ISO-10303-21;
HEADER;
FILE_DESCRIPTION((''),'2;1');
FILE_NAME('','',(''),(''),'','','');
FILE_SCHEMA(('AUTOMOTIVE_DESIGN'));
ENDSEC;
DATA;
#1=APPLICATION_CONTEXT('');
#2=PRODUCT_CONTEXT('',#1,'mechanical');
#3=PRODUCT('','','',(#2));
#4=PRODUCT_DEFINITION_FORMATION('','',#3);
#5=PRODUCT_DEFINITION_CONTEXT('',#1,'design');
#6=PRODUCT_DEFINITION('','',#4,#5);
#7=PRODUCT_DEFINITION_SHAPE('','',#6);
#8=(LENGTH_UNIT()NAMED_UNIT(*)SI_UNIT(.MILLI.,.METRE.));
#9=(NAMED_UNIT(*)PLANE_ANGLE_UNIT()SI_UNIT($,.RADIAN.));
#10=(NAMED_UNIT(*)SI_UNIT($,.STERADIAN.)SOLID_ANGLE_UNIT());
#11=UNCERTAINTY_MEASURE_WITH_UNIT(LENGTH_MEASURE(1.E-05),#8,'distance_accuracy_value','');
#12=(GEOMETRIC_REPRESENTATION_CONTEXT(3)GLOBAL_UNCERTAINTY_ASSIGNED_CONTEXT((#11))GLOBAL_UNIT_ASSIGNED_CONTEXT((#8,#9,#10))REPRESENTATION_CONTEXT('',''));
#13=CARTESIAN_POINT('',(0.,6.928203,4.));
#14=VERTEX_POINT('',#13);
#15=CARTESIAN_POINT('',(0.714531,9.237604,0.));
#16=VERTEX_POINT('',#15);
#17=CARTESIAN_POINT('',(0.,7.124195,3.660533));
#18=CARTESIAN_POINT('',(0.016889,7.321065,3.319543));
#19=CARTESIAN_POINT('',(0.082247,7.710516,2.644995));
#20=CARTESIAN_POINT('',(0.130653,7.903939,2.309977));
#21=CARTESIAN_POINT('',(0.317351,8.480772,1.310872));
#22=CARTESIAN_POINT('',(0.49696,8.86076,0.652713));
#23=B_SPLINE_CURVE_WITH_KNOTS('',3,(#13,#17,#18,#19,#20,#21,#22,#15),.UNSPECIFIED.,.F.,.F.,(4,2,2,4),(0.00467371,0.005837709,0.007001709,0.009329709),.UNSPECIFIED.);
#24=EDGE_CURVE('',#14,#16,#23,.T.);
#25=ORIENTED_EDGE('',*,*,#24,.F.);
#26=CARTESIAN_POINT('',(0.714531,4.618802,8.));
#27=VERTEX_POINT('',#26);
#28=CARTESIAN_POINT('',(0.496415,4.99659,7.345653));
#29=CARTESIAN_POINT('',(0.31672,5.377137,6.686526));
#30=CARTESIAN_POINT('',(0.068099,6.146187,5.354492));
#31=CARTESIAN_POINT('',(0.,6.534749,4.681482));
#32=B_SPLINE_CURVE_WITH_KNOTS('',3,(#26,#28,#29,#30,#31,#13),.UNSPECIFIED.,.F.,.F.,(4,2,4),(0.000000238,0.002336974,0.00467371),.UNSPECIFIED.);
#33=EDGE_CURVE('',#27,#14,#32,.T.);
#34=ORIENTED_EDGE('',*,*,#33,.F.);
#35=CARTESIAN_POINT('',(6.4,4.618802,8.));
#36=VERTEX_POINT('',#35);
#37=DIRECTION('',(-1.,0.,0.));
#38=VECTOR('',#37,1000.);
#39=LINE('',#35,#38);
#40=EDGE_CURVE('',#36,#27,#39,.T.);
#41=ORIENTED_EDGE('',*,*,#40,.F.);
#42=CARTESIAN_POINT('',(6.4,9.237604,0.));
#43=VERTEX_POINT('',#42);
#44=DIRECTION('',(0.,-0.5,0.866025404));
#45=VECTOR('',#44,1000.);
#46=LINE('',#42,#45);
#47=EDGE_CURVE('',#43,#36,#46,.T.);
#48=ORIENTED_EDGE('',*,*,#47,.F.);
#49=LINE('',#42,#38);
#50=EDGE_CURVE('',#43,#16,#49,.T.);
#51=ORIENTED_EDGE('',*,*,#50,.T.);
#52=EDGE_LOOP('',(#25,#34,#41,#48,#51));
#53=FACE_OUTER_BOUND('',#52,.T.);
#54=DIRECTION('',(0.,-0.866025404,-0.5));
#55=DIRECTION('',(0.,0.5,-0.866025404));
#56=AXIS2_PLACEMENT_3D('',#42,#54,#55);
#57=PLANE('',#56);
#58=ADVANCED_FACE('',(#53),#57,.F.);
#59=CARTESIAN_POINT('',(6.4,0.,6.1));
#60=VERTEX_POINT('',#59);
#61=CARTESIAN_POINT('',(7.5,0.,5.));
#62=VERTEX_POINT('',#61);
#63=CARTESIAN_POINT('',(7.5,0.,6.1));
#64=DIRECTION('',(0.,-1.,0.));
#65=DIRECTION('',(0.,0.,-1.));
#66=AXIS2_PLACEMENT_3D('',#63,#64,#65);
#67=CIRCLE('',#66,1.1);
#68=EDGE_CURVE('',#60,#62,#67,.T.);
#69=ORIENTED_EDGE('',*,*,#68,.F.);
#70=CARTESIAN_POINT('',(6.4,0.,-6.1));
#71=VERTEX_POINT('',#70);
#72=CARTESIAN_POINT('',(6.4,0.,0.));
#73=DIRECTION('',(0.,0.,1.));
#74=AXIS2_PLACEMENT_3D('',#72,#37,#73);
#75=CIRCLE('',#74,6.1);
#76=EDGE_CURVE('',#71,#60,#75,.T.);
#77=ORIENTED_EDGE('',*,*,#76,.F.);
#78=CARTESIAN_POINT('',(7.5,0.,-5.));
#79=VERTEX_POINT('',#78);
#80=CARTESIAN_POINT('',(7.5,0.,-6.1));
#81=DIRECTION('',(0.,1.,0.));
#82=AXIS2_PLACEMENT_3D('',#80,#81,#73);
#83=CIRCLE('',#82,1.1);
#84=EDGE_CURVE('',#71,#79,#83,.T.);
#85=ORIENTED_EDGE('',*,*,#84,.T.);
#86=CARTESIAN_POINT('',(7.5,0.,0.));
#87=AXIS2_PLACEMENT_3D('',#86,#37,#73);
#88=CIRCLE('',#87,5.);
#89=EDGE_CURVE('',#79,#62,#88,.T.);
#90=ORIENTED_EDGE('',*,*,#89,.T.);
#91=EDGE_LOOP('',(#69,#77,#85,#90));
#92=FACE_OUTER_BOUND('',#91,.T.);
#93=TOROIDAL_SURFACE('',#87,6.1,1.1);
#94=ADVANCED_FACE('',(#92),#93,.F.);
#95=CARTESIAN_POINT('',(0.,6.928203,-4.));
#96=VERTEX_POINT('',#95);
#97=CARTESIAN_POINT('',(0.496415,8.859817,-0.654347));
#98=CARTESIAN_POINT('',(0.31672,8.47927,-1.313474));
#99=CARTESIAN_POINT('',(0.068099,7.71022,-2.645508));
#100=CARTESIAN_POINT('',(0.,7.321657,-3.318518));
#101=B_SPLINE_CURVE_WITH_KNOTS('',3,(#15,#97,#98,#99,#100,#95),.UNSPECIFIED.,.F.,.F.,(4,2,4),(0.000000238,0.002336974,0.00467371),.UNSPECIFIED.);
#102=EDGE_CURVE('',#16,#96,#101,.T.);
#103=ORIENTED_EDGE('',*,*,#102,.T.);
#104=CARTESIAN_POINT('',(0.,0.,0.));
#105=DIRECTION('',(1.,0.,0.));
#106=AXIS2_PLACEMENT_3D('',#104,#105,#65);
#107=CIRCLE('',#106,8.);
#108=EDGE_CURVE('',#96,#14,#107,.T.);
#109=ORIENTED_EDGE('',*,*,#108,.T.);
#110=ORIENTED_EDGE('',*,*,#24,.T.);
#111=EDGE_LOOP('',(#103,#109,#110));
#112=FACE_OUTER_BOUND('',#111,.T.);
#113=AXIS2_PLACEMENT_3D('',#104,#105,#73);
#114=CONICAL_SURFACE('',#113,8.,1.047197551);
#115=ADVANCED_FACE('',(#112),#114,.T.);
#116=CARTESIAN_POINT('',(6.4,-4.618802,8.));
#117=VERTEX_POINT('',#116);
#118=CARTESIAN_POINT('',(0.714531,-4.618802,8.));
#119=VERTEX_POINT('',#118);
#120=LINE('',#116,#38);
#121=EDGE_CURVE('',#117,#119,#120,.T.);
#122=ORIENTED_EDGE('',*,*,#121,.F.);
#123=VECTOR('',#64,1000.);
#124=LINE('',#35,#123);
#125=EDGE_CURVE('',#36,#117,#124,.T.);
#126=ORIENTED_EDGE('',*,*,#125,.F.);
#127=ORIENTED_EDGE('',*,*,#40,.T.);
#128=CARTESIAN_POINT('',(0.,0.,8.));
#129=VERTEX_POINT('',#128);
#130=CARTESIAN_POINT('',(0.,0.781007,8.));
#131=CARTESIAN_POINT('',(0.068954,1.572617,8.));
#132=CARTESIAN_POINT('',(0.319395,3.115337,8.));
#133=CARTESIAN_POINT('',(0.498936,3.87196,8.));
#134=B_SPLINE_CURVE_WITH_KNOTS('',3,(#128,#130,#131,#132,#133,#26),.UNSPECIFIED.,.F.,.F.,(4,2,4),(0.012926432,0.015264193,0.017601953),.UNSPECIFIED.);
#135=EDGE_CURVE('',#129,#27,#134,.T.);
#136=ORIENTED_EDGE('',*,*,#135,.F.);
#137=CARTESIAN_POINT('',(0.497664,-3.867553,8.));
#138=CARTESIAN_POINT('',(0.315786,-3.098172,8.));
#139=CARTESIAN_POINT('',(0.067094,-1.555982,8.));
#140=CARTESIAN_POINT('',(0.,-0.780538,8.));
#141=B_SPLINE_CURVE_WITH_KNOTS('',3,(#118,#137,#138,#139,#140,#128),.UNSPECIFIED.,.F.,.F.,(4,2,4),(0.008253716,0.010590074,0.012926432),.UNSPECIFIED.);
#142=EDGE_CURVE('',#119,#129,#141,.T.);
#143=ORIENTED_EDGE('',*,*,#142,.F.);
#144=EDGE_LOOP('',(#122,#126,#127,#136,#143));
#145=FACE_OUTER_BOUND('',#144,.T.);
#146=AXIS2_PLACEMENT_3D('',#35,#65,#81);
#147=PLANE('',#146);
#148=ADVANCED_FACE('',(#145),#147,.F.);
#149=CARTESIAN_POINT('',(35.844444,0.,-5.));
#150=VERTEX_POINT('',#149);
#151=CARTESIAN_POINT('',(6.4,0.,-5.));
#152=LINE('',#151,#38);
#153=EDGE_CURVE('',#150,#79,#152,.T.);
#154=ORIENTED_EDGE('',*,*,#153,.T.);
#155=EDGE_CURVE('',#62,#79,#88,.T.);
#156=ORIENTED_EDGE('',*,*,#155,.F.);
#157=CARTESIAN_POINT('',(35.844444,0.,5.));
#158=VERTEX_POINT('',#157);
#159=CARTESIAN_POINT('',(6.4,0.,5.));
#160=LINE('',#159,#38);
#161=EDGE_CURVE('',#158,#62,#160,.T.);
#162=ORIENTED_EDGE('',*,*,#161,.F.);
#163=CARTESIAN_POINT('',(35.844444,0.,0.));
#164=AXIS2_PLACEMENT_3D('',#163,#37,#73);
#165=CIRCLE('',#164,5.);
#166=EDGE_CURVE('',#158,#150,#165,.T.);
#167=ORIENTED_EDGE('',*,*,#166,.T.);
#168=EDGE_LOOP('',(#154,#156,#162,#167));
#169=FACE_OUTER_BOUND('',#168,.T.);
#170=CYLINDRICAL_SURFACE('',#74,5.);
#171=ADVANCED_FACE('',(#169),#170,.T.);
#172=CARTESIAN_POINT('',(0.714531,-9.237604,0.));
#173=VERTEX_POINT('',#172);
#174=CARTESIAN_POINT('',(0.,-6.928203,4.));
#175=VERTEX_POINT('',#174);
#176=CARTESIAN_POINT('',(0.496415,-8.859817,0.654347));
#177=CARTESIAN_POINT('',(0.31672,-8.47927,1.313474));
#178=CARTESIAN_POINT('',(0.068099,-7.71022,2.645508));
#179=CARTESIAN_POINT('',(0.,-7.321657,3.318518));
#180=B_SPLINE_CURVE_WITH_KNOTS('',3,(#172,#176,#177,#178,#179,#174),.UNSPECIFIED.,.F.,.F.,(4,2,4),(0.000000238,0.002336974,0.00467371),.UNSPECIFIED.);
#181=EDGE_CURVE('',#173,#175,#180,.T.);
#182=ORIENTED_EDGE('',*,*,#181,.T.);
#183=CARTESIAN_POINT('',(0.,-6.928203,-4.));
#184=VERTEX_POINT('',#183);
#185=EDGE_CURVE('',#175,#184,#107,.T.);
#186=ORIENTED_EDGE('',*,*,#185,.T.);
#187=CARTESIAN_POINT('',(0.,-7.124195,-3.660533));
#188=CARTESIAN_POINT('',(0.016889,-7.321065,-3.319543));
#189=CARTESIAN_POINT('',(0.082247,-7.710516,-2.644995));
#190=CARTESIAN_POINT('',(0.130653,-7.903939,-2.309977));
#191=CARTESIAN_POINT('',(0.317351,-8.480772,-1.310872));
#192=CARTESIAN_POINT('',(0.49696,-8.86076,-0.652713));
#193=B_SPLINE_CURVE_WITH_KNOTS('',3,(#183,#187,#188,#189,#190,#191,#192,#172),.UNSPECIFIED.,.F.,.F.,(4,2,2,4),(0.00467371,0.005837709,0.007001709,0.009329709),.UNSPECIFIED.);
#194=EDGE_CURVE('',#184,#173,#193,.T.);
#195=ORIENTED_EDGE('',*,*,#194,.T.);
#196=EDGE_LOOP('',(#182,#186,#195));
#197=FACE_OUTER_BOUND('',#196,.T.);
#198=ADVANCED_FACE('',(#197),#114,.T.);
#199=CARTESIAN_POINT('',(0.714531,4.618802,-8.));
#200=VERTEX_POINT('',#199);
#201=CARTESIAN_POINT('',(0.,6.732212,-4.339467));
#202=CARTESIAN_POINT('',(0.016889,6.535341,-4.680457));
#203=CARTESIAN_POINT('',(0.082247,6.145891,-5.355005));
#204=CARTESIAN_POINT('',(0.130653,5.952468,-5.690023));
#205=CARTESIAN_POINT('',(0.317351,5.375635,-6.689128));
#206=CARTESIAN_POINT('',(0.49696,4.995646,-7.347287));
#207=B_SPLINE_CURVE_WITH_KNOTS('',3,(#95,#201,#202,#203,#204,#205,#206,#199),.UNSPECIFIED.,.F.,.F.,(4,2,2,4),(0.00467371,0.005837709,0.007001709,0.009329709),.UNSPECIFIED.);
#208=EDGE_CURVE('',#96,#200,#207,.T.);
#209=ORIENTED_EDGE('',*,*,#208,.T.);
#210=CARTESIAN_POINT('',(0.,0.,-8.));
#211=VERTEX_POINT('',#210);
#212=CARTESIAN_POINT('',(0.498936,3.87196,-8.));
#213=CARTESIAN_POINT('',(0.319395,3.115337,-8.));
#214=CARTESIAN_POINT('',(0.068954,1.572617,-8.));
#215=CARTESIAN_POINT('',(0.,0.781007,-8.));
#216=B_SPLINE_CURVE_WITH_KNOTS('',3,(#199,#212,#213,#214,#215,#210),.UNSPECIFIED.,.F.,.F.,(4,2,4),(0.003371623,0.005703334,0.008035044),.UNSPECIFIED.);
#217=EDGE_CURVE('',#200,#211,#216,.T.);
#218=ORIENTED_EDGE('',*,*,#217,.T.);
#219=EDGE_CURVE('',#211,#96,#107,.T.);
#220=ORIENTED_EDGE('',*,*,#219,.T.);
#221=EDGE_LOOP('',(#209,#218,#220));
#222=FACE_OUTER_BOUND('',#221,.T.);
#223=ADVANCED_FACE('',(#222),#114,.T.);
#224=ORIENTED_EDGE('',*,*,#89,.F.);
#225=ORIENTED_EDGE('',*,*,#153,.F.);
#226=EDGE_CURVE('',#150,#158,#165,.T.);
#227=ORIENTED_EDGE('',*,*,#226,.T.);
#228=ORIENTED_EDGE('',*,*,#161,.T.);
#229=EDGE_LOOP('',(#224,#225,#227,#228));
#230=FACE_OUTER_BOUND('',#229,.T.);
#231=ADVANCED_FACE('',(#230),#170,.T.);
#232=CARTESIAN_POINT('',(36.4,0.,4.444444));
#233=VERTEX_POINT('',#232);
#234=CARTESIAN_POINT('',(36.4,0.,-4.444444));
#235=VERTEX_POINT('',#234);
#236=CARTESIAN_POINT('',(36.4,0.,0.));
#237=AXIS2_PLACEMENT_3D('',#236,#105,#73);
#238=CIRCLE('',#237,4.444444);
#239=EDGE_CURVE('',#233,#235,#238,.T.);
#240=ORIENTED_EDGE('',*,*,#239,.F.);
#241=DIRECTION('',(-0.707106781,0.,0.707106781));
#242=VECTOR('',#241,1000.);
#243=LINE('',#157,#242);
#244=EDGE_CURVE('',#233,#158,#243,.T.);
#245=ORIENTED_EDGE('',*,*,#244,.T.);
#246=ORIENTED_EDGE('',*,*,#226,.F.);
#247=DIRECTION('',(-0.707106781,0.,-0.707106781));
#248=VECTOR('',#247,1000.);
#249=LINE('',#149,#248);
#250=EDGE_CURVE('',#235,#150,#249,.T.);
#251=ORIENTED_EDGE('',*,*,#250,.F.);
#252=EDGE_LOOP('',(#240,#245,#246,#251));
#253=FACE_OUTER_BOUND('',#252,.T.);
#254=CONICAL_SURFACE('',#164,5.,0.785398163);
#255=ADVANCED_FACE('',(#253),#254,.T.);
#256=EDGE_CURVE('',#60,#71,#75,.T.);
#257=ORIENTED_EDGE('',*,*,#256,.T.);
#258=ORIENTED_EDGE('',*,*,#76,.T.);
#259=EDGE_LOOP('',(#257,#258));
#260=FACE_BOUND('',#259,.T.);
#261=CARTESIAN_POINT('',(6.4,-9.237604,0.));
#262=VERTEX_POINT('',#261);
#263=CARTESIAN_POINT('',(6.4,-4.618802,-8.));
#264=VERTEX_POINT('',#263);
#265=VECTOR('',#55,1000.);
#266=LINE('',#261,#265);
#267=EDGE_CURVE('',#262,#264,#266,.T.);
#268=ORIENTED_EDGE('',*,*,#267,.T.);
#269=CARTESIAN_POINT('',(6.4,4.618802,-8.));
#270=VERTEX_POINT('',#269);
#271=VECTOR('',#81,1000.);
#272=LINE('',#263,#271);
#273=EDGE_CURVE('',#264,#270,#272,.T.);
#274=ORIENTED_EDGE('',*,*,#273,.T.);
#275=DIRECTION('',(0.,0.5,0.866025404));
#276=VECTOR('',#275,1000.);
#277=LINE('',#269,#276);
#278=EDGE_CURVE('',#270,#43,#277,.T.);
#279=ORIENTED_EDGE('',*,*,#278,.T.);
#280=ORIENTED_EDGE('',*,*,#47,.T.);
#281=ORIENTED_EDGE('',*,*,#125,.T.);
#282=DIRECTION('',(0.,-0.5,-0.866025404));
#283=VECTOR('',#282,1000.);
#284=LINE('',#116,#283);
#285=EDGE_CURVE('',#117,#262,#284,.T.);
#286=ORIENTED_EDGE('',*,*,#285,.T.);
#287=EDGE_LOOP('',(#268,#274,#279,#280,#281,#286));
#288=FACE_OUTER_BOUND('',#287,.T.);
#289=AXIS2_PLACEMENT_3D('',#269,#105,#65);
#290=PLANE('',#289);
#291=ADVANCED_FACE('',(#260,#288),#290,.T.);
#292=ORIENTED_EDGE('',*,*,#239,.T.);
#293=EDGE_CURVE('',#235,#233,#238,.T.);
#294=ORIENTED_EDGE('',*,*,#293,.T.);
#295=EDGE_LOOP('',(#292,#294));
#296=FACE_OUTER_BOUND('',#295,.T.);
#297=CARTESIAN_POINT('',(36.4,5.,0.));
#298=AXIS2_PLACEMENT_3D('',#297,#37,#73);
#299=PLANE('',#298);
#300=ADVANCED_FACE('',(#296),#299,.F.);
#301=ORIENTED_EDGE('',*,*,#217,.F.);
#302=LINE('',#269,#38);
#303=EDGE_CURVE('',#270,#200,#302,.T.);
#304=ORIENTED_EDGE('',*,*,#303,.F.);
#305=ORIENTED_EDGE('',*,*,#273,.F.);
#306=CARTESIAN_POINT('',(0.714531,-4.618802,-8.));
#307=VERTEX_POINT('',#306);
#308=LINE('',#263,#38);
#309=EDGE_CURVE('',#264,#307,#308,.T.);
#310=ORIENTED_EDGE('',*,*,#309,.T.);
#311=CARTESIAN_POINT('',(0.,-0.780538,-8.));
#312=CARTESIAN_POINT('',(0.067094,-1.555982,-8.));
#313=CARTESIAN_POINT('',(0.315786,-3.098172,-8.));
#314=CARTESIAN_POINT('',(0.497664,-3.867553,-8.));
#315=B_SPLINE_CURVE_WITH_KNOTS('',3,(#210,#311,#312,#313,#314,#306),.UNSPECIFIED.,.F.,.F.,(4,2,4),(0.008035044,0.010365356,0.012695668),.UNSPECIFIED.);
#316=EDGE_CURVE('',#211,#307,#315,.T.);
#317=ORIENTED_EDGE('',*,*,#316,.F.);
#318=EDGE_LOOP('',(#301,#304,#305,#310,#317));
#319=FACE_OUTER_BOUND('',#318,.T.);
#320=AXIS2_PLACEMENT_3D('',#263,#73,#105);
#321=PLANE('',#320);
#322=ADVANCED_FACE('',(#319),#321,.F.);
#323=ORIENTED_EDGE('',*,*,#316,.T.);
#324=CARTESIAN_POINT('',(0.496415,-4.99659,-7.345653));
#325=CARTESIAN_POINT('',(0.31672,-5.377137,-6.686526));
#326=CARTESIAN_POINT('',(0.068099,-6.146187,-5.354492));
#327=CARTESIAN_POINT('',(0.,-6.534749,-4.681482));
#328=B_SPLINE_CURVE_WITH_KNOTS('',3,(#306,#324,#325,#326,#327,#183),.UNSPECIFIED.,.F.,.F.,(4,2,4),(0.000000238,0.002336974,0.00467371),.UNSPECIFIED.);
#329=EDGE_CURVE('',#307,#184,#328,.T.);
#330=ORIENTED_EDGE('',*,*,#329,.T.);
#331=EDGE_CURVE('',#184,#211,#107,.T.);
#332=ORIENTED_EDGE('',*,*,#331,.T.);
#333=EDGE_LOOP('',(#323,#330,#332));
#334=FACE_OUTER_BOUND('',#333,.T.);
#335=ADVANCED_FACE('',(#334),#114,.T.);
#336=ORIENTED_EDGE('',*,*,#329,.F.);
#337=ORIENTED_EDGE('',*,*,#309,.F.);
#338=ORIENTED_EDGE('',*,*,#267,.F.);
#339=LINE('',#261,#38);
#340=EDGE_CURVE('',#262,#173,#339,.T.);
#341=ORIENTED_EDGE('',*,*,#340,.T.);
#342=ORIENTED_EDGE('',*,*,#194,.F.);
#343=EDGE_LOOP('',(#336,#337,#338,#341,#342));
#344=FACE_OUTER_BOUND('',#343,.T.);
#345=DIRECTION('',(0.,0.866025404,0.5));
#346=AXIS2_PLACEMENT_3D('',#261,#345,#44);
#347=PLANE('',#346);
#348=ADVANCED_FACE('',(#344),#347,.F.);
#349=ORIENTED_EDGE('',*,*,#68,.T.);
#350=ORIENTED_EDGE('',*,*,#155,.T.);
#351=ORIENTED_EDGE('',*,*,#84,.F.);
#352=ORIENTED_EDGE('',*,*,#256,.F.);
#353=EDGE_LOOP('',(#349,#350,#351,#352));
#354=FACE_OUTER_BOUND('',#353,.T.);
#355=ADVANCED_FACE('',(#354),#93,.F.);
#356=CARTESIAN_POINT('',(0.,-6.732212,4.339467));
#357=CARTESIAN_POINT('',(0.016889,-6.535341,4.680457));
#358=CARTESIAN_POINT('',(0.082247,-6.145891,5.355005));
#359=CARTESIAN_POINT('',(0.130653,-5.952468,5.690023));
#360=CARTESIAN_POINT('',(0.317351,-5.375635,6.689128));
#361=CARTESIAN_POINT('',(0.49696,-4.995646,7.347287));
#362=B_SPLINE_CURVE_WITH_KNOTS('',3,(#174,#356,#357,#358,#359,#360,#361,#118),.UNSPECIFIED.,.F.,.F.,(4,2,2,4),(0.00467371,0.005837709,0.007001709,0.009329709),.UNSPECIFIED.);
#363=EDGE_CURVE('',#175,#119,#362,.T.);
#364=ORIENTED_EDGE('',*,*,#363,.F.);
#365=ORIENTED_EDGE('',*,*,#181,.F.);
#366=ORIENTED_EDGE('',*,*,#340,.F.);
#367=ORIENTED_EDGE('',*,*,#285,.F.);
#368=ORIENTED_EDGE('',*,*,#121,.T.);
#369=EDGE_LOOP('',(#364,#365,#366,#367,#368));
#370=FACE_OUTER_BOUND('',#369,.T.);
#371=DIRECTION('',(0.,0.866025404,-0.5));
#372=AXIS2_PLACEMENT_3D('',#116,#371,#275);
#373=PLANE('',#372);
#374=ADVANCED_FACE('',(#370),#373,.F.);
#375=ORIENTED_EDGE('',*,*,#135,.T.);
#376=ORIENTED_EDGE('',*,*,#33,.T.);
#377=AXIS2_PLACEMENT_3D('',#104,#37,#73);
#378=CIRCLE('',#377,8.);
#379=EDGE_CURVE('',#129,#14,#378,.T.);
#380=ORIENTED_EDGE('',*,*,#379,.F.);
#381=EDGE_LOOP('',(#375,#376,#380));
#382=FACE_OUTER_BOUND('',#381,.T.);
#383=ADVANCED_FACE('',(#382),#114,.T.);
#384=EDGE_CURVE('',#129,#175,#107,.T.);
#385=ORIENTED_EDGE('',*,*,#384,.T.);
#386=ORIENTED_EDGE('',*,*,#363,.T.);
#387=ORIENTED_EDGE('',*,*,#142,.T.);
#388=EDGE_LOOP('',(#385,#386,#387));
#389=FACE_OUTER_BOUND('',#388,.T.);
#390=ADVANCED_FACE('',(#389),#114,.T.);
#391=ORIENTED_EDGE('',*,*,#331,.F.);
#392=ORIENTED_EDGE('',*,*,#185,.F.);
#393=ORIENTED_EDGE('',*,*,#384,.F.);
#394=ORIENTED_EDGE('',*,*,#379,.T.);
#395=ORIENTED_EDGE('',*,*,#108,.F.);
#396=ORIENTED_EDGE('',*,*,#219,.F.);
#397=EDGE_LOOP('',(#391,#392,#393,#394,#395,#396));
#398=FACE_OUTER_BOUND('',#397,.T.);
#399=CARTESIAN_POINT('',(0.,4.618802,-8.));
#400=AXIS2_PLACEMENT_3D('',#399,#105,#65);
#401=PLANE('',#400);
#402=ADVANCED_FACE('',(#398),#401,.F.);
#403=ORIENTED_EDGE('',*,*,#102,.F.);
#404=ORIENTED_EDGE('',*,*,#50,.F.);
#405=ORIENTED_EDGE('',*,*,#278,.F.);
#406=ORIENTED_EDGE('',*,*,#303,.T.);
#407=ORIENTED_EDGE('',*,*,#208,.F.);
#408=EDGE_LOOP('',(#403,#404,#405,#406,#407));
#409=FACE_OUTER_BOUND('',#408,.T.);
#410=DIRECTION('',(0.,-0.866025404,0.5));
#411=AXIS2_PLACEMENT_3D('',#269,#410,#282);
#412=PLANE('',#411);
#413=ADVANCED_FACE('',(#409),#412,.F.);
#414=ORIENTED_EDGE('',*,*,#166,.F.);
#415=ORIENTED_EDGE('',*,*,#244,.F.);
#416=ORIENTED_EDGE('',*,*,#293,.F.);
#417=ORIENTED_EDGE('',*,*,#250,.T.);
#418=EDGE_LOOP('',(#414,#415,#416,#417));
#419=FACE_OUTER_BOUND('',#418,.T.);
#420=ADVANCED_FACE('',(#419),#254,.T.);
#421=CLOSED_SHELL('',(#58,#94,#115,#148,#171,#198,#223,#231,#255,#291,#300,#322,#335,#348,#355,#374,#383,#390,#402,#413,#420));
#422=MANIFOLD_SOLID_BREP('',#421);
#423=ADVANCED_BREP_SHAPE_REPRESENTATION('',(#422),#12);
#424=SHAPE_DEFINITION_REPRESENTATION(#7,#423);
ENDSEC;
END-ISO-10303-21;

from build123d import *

# Parameters (mm, degrees)
BOSS_EXTRUDE1_DEPTH = 6.4
SKETCH4_R           = 17.59
SKETCH4_R_2         = 8
CUT_EXTRUDE1_DEPTH  = 0.8
CUT_EXTRUDE1_DRAFT  = -60
CHAMFER2_SIZE       = 0.555555556


with BuildPart() as part:
    # Sketch3 → Boss-Extrude1 (new body)
    with BuildSketch(Plane(origin=(0, 0, 0), x_dir=(0, 0, -1), z_dir=(1, 0, 0))):
        Polygon((8, 4.618802154), (0, 9.237604307), (-8, 4.618802154), (-8, -4.618802154), (0, -9.237604307), (8, -4.618802154), align=None)
    extrude(amount=BOSS_EXTRUDE1_DEPTH)


with BuildPart() as cut_extrude1_tool:
    # Sketch4 → Cut-Extrude1 (with draft: the straight prism first)
    with BuildSketch(Plane.ZY):
        Circle(SKETCH4_R)
        Circle(SKETCH4_R_2, mode=Mode.SUBTRACT)
    extrude(amount=-CUT_EXTRUDE1_DEPTH)
    # Cut-Extrude1: the draft: its side faces are tilted about the plane it starts from
    cut_extrude1_sides = [cut_extrude1_tool.faces().sort_by_distance(p)[0] for p in [
        (0.4, 0, -17.59),
        (0.4, 0, -8),
    ]]
    draft(cut_extrude1_sides, Plane.ZY, CUT_EXTRUDE1_DRAFT)


with BuildPart() as part_1:
    add(part.part)

    # Cut-Extrude1: cut by cut_extrude1_tool
    add(cut_extrude1_tool.part, mode=Mode.SUBTRACT)

    # Sketch5 → Revolve1 (revolve)
    with BuildSketch(Plane.XY, mode=Mode.PRIVATE) as revolve1_sk:
        with BuildLine():
            Line((7.5, 5), (36.4, 5))
            Line((36.4, 5), (36.4, 0))
            Line((36.4, 0), (6.4, 0))
            Line((6.4, 0), (6.4, 6.1))
            ThreePointArc((6.4, 6.1), (6.722182541, 5.322182541), (7.5, 5))
        make_face()
    revolve(revolve1_sk.sketch.rotate(Axis((6.4, 0, 0), (1, 0, 0)), 90), axis=Axis((6.4, 0, 0), (1, 0, 0)))

    # Chamfer2
    chamfer2_edges = [part_1.edges().sort_by_distance(p)[0] for p in [
        (36.4, 0, -5),
    ]]
    chamfer(chamfer2_edges, length=CHAMFER2_SIZE)


solid = part_1.part
